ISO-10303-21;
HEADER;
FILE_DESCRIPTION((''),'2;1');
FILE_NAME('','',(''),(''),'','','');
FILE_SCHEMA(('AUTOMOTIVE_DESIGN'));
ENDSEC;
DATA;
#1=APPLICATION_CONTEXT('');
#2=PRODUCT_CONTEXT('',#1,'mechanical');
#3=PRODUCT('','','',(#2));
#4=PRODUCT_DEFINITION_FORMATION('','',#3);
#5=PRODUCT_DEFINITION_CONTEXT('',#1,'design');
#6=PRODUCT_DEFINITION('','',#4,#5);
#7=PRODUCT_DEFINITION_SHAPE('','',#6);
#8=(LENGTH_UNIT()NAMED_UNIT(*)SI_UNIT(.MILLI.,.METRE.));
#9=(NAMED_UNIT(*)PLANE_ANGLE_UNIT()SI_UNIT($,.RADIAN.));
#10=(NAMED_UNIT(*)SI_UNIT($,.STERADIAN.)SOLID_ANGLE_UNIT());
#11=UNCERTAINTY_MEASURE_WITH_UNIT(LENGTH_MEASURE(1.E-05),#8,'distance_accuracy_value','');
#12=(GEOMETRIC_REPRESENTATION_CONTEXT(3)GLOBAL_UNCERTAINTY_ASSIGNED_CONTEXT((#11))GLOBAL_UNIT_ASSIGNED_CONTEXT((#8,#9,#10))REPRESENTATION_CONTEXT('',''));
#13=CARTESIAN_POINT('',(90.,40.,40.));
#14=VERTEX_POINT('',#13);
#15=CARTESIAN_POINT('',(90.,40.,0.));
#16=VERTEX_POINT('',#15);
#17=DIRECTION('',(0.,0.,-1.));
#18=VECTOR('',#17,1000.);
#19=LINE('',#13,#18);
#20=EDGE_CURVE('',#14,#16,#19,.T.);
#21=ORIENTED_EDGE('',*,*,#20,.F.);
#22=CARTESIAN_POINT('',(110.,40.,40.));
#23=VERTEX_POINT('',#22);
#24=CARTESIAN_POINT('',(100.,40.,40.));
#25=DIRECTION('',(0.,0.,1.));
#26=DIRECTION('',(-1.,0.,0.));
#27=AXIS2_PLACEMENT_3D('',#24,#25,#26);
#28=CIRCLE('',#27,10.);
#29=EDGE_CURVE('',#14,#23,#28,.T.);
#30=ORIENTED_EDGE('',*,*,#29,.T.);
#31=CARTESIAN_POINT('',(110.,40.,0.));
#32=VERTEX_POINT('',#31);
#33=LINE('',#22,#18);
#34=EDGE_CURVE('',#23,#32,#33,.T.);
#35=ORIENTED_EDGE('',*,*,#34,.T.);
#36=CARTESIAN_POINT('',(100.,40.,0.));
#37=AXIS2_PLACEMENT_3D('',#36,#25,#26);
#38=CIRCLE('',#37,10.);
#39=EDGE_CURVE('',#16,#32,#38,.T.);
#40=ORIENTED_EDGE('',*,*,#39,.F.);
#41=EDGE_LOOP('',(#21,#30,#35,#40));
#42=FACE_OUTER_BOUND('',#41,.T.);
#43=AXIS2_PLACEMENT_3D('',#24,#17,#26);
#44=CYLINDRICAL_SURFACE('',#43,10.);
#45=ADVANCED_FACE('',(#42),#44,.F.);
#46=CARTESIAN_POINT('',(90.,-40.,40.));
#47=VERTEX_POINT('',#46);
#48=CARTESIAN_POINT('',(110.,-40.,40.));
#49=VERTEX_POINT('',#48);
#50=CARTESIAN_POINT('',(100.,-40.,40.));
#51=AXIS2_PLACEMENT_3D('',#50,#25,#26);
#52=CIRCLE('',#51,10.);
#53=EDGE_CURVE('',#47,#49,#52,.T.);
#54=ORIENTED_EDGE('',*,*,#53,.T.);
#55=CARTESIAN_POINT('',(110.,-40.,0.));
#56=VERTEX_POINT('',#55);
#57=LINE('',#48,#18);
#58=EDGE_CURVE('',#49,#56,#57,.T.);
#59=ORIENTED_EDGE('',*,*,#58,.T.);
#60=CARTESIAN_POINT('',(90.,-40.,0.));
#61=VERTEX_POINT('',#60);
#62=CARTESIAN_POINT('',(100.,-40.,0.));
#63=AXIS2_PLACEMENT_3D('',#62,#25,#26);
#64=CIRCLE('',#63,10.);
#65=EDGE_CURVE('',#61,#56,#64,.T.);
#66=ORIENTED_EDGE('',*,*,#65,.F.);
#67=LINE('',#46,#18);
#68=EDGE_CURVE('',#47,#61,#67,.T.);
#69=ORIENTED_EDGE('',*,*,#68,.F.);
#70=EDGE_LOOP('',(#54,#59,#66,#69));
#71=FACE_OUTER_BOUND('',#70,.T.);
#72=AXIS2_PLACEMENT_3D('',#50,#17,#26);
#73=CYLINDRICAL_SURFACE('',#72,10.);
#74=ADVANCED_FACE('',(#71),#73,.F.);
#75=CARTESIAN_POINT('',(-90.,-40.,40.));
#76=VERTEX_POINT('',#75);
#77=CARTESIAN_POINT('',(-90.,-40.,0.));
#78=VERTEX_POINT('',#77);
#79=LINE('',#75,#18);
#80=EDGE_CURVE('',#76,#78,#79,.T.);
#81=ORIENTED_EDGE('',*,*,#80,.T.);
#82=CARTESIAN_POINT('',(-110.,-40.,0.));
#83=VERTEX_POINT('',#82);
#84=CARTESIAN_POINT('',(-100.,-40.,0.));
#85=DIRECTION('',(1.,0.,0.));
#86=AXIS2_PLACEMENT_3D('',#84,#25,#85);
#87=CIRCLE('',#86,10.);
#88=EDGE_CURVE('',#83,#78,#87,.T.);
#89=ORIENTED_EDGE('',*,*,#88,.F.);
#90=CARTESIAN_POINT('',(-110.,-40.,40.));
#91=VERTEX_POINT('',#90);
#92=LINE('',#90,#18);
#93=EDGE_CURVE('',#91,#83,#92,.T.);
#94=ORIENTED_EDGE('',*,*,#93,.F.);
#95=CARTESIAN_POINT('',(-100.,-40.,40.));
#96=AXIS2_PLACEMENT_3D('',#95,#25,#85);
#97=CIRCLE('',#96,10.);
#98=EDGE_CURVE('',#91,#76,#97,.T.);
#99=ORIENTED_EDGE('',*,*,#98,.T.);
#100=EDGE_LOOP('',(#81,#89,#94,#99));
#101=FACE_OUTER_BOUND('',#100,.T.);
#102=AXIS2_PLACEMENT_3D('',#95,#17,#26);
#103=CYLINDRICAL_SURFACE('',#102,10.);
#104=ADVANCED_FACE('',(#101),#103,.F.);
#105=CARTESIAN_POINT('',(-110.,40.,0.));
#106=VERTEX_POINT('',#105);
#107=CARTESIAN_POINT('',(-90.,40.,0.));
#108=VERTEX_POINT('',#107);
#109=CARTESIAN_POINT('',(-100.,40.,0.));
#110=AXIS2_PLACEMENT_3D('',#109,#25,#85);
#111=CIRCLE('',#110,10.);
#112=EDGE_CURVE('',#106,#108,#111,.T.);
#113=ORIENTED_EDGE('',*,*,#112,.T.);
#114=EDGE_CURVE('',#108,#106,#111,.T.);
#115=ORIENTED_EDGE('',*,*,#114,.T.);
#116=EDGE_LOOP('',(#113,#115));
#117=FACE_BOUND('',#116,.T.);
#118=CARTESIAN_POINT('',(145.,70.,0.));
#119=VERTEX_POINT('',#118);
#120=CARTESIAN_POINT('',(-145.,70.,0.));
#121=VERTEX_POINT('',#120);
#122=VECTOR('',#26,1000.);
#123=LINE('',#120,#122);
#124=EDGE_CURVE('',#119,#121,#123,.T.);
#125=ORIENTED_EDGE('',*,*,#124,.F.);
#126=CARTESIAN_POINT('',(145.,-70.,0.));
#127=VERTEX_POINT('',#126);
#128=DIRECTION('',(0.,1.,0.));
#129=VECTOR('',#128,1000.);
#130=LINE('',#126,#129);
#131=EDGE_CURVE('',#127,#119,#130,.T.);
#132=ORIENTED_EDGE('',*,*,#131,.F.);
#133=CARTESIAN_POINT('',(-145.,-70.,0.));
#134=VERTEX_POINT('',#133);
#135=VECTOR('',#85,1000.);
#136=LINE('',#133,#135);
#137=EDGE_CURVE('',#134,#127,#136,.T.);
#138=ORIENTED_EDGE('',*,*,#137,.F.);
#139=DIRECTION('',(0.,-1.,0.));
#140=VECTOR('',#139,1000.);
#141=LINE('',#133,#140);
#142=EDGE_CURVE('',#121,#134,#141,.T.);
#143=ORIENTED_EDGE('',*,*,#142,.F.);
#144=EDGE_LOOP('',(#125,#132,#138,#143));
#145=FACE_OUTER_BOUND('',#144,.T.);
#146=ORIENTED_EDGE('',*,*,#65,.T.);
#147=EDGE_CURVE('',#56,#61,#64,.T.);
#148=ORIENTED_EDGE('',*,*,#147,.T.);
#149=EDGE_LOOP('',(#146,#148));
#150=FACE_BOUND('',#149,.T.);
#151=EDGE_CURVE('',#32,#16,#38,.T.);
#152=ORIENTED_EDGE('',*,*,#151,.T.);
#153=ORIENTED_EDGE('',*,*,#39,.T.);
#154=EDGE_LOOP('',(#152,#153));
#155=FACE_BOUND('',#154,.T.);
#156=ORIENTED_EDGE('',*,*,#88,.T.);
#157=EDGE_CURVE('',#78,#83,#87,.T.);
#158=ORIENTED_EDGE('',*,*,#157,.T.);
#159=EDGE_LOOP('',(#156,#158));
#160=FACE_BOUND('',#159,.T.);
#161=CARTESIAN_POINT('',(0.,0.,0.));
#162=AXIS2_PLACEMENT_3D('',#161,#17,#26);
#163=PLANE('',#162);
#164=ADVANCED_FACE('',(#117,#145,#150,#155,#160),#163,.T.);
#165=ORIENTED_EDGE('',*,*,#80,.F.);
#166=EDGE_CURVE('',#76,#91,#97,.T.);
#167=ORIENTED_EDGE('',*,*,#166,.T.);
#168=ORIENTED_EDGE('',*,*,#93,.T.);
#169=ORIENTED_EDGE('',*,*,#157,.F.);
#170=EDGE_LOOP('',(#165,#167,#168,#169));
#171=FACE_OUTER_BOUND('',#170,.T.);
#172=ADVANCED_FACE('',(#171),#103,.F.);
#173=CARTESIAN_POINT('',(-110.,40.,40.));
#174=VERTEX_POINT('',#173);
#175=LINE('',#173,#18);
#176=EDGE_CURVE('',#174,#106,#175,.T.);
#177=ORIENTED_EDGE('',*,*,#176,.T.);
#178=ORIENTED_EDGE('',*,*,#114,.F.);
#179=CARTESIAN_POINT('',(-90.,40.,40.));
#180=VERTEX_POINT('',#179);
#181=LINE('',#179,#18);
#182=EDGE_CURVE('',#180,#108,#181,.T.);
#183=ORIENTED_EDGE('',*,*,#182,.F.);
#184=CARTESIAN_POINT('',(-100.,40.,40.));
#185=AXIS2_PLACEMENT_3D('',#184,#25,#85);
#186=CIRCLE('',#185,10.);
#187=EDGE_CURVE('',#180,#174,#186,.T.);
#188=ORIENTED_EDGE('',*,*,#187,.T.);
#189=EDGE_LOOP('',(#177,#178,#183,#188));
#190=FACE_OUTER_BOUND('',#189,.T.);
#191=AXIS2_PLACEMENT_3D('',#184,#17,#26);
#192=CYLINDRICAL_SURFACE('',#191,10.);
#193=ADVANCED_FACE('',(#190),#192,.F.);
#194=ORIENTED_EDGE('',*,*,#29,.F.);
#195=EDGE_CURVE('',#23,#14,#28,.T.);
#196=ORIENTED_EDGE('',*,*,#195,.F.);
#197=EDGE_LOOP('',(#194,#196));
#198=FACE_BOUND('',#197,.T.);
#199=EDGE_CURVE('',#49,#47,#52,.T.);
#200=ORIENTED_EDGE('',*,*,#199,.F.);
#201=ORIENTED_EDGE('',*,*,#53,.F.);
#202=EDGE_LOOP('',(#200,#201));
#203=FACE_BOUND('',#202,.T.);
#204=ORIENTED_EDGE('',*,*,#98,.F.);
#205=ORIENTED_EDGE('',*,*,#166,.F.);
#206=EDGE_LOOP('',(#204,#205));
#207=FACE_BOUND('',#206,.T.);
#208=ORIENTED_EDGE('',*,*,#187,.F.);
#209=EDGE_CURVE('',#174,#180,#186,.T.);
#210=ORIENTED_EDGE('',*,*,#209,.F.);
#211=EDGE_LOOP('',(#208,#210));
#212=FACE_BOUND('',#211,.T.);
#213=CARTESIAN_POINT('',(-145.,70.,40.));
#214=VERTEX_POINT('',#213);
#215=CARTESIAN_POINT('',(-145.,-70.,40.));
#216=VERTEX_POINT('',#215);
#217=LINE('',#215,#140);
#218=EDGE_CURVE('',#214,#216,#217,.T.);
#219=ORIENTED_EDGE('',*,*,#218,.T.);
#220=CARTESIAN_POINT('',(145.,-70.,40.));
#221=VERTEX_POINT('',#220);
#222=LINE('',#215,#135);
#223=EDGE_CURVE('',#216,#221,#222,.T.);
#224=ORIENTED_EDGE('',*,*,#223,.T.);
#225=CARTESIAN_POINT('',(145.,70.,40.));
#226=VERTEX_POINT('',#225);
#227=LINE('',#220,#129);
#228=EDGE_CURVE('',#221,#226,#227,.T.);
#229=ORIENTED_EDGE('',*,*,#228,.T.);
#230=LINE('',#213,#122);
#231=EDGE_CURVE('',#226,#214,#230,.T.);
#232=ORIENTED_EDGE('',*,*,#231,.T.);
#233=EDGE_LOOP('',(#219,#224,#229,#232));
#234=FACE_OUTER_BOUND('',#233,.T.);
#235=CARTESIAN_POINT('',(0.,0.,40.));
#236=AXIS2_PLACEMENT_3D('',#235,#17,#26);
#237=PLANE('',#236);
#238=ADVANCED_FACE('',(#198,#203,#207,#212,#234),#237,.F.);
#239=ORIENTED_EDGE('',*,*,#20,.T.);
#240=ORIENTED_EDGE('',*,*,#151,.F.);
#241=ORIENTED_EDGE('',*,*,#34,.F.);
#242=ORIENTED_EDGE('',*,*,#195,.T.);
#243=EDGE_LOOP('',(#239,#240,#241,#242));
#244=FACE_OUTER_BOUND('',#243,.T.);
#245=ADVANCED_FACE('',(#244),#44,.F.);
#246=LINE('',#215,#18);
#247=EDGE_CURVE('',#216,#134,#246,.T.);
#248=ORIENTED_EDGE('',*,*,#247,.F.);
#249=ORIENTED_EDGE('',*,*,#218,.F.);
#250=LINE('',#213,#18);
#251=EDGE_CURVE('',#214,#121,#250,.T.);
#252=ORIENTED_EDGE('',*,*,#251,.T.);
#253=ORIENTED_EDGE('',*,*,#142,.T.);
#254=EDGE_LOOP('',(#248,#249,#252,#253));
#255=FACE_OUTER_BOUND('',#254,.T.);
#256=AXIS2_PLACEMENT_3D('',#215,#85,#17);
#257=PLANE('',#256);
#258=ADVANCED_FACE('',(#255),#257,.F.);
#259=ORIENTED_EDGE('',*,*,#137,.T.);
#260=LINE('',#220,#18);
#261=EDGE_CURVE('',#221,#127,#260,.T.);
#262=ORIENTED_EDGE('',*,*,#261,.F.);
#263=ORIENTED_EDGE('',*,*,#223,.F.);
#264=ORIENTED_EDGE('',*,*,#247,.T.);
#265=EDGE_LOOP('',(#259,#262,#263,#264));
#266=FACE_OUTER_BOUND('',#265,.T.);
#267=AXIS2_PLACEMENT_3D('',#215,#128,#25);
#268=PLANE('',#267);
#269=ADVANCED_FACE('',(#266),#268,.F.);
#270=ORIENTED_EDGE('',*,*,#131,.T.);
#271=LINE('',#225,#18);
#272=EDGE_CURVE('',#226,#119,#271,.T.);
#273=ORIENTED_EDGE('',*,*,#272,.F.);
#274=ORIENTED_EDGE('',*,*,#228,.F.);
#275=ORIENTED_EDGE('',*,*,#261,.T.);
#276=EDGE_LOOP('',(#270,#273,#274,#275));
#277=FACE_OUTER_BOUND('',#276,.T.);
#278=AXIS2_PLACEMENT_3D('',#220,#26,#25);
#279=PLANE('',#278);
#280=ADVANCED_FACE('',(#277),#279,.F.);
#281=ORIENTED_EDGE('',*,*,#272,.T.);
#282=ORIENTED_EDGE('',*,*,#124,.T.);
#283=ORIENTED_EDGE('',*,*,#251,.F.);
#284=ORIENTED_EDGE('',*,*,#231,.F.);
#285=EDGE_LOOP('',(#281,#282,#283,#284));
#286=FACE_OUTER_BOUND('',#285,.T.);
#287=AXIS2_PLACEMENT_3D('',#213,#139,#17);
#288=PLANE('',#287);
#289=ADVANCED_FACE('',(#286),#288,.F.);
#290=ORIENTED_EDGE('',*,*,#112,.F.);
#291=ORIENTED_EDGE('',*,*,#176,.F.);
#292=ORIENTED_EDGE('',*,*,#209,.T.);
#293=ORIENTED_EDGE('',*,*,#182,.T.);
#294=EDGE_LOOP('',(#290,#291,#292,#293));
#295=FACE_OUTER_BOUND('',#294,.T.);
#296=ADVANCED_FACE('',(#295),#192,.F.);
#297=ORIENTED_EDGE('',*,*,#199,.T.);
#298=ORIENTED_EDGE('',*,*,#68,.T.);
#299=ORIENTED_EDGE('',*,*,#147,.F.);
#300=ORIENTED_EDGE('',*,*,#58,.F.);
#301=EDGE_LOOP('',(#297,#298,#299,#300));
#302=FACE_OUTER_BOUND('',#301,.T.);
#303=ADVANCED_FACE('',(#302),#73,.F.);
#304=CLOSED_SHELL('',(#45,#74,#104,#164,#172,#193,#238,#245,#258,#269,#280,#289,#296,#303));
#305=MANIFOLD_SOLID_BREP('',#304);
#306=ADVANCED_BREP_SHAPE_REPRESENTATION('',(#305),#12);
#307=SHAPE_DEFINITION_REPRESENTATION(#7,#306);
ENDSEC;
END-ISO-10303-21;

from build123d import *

# Parameters (mm, degrees)
SKETCH1_W           = 290
SKETCH1_H           = 140
SKETCH1_R           = 10
BOSS_EXTRUDE1_DEPTH = 40


with BuildPart() as part:
    # Sketch1 → Boss-Extrude1 (new body)
    with BuildSketch(Plane.XY):
        Rectangle(SKETCH1_W, SKETCH1_H)
        with Locations((-100, 40)):
            Circle(SKETCH1_R, mode=Mode.SUBTRACT)
        with Locations((-100, -40)):
            Circle(SKETCH1_R, mode=Mode.SUBTRACT)
        with Locations(Location((100, -40, 0), (0, 0, 180))):
            Circle(SKETCH1_R, mode=Mode.SUBTRACT)
        with Locations(Location((100, 40, 0), (0, 0, 180))):
            Circle(SKETCH1_R, mode=Mode.SUBTRACT)
    extrude(amount=BOSS_EXTRUDE1_DEPTH)


solid = part.part
